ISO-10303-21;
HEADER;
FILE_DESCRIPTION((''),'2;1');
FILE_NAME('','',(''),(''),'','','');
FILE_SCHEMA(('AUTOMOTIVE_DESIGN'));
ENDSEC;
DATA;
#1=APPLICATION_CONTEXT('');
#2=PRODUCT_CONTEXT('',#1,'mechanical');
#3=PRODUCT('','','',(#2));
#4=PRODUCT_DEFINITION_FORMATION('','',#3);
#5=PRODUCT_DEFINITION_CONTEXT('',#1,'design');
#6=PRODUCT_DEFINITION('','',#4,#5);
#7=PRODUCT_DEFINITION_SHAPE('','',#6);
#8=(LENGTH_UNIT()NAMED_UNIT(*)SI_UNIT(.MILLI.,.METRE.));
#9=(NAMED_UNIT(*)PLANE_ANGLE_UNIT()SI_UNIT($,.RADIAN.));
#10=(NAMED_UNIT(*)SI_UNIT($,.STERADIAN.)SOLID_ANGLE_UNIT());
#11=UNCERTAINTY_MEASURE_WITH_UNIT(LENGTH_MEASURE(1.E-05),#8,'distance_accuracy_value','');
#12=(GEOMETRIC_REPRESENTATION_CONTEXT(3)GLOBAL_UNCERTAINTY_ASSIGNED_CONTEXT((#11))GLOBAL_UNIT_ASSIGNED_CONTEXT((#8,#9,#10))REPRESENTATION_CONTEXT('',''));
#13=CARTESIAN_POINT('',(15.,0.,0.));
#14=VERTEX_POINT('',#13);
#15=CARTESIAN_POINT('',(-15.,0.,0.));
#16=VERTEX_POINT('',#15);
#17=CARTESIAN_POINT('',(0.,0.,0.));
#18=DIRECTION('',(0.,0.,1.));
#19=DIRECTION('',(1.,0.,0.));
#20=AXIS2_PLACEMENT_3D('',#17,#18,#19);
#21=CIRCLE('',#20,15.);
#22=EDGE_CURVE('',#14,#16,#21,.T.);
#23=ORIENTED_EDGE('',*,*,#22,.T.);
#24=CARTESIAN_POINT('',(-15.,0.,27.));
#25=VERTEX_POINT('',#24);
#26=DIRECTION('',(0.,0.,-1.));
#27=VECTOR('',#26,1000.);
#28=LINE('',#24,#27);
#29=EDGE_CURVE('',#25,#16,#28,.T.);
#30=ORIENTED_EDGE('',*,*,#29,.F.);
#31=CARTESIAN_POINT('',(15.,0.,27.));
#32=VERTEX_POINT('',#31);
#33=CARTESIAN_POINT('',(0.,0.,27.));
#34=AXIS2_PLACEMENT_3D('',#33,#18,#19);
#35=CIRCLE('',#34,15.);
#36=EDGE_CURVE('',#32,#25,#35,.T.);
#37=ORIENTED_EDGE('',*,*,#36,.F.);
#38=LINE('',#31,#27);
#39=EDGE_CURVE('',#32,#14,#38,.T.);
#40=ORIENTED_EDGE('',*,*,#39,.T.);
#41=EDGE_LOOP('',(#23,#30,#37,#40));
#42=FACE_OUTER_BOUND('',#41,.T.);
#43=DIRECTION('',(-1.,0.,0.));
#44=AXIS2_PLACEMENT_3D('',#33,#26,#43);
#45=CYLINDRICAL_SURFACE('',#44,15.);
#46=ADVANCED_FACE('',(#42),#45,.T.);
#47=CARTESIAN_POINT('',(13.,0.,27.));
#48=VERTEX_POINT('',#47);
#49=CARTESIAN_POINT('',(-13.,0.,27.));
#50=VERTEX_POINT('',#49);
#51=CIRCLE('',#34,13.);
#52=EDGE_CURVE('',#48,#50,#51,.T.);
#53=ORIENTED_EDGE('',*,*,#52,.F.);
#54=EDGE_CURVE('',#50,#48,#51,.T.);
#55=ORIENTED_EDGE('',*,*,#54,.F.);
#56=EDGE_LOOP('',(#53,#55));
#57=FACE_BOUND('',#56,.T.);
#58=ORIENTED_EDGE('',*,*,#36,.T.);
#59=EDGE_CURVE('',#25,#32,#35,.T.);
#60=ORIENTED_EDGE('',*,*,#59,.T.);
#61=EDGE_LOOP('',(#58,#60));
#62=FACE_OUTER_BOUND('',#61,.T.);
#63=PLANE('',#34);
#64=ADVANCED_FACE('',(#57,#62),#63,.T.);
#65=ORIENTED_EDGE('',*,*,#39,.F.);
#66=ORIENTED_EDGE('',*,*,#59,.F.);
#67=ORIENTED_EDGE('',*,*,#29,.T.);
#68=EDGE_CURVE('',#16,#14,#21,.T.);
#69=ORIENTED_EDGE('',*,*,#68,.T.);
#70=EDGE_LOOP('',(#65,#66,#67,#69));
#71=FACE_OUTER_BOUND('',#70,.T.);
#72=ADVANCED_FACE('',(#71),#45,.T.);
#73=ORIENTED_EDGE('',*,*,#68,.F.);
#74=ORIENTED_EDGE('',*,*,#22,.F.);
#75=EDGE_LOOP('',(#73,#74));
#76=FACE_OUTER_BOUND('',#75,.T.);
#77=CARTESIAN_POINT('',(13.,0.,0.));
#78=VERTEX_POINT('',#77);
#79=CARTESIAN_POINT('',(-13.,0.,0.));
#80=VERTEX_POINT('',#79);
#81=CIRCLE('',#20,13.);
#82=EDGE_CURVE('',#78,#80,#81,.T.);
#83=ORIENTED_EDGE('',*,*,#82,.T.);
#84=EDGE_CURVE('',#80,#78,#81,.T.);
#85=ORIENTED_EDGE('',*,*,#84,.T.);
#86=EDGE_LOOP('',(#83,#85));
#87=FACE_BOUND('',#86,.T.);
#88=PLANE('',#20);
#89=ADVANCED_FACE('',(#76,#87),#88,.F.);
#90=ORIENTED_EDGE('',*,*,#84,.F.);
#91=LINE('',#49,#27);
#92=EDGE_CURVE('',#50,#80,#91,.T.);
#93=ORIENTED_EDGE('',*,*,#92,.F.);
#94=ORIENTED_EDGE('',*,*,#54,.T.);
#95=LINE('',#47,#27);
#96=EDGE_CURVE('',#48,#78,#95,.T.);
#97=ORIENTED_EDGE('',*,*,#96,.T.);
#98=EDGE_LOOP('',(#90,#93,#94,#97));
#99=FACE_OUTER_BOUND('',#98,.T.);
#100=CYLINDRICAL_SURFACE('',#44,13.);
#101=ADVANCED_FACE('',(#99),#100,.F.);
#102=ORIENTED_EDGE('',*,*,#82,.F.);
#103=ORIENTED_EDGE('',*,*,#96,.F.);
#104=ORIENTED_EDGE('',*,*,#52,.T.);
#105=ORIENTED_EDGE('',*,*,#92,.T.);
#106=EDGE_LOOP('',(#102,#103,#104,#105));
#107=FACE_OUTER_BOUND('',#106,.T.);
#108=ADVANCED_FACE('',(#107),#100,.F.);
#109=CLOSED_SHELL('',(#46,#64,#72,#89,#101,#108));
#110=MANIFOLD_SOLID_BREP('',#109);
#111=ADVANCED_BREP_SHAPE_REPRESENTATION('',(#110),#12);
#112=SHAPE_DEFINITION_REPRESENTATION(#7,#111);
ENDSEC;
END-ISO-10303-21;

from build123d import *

# Parameters (mm, degrees)
SKETCH1_R           = 15
SKETCH1_R_2         = 13
BOSS_EXTRUDE1_DEPTH = 27


with BuildPart() as part:
    # Sketch1 → Boss-Extrude1 (new body)
    with BuildSketch(Plane.XY):
        Circle(SKETCH1_R)
        Circle(SKETCH1_R_2, mode=Mode.SUBTRACT)
    extrude(amount=BOSS_EXTRUDE1_DEPTH)


solid = part.part
